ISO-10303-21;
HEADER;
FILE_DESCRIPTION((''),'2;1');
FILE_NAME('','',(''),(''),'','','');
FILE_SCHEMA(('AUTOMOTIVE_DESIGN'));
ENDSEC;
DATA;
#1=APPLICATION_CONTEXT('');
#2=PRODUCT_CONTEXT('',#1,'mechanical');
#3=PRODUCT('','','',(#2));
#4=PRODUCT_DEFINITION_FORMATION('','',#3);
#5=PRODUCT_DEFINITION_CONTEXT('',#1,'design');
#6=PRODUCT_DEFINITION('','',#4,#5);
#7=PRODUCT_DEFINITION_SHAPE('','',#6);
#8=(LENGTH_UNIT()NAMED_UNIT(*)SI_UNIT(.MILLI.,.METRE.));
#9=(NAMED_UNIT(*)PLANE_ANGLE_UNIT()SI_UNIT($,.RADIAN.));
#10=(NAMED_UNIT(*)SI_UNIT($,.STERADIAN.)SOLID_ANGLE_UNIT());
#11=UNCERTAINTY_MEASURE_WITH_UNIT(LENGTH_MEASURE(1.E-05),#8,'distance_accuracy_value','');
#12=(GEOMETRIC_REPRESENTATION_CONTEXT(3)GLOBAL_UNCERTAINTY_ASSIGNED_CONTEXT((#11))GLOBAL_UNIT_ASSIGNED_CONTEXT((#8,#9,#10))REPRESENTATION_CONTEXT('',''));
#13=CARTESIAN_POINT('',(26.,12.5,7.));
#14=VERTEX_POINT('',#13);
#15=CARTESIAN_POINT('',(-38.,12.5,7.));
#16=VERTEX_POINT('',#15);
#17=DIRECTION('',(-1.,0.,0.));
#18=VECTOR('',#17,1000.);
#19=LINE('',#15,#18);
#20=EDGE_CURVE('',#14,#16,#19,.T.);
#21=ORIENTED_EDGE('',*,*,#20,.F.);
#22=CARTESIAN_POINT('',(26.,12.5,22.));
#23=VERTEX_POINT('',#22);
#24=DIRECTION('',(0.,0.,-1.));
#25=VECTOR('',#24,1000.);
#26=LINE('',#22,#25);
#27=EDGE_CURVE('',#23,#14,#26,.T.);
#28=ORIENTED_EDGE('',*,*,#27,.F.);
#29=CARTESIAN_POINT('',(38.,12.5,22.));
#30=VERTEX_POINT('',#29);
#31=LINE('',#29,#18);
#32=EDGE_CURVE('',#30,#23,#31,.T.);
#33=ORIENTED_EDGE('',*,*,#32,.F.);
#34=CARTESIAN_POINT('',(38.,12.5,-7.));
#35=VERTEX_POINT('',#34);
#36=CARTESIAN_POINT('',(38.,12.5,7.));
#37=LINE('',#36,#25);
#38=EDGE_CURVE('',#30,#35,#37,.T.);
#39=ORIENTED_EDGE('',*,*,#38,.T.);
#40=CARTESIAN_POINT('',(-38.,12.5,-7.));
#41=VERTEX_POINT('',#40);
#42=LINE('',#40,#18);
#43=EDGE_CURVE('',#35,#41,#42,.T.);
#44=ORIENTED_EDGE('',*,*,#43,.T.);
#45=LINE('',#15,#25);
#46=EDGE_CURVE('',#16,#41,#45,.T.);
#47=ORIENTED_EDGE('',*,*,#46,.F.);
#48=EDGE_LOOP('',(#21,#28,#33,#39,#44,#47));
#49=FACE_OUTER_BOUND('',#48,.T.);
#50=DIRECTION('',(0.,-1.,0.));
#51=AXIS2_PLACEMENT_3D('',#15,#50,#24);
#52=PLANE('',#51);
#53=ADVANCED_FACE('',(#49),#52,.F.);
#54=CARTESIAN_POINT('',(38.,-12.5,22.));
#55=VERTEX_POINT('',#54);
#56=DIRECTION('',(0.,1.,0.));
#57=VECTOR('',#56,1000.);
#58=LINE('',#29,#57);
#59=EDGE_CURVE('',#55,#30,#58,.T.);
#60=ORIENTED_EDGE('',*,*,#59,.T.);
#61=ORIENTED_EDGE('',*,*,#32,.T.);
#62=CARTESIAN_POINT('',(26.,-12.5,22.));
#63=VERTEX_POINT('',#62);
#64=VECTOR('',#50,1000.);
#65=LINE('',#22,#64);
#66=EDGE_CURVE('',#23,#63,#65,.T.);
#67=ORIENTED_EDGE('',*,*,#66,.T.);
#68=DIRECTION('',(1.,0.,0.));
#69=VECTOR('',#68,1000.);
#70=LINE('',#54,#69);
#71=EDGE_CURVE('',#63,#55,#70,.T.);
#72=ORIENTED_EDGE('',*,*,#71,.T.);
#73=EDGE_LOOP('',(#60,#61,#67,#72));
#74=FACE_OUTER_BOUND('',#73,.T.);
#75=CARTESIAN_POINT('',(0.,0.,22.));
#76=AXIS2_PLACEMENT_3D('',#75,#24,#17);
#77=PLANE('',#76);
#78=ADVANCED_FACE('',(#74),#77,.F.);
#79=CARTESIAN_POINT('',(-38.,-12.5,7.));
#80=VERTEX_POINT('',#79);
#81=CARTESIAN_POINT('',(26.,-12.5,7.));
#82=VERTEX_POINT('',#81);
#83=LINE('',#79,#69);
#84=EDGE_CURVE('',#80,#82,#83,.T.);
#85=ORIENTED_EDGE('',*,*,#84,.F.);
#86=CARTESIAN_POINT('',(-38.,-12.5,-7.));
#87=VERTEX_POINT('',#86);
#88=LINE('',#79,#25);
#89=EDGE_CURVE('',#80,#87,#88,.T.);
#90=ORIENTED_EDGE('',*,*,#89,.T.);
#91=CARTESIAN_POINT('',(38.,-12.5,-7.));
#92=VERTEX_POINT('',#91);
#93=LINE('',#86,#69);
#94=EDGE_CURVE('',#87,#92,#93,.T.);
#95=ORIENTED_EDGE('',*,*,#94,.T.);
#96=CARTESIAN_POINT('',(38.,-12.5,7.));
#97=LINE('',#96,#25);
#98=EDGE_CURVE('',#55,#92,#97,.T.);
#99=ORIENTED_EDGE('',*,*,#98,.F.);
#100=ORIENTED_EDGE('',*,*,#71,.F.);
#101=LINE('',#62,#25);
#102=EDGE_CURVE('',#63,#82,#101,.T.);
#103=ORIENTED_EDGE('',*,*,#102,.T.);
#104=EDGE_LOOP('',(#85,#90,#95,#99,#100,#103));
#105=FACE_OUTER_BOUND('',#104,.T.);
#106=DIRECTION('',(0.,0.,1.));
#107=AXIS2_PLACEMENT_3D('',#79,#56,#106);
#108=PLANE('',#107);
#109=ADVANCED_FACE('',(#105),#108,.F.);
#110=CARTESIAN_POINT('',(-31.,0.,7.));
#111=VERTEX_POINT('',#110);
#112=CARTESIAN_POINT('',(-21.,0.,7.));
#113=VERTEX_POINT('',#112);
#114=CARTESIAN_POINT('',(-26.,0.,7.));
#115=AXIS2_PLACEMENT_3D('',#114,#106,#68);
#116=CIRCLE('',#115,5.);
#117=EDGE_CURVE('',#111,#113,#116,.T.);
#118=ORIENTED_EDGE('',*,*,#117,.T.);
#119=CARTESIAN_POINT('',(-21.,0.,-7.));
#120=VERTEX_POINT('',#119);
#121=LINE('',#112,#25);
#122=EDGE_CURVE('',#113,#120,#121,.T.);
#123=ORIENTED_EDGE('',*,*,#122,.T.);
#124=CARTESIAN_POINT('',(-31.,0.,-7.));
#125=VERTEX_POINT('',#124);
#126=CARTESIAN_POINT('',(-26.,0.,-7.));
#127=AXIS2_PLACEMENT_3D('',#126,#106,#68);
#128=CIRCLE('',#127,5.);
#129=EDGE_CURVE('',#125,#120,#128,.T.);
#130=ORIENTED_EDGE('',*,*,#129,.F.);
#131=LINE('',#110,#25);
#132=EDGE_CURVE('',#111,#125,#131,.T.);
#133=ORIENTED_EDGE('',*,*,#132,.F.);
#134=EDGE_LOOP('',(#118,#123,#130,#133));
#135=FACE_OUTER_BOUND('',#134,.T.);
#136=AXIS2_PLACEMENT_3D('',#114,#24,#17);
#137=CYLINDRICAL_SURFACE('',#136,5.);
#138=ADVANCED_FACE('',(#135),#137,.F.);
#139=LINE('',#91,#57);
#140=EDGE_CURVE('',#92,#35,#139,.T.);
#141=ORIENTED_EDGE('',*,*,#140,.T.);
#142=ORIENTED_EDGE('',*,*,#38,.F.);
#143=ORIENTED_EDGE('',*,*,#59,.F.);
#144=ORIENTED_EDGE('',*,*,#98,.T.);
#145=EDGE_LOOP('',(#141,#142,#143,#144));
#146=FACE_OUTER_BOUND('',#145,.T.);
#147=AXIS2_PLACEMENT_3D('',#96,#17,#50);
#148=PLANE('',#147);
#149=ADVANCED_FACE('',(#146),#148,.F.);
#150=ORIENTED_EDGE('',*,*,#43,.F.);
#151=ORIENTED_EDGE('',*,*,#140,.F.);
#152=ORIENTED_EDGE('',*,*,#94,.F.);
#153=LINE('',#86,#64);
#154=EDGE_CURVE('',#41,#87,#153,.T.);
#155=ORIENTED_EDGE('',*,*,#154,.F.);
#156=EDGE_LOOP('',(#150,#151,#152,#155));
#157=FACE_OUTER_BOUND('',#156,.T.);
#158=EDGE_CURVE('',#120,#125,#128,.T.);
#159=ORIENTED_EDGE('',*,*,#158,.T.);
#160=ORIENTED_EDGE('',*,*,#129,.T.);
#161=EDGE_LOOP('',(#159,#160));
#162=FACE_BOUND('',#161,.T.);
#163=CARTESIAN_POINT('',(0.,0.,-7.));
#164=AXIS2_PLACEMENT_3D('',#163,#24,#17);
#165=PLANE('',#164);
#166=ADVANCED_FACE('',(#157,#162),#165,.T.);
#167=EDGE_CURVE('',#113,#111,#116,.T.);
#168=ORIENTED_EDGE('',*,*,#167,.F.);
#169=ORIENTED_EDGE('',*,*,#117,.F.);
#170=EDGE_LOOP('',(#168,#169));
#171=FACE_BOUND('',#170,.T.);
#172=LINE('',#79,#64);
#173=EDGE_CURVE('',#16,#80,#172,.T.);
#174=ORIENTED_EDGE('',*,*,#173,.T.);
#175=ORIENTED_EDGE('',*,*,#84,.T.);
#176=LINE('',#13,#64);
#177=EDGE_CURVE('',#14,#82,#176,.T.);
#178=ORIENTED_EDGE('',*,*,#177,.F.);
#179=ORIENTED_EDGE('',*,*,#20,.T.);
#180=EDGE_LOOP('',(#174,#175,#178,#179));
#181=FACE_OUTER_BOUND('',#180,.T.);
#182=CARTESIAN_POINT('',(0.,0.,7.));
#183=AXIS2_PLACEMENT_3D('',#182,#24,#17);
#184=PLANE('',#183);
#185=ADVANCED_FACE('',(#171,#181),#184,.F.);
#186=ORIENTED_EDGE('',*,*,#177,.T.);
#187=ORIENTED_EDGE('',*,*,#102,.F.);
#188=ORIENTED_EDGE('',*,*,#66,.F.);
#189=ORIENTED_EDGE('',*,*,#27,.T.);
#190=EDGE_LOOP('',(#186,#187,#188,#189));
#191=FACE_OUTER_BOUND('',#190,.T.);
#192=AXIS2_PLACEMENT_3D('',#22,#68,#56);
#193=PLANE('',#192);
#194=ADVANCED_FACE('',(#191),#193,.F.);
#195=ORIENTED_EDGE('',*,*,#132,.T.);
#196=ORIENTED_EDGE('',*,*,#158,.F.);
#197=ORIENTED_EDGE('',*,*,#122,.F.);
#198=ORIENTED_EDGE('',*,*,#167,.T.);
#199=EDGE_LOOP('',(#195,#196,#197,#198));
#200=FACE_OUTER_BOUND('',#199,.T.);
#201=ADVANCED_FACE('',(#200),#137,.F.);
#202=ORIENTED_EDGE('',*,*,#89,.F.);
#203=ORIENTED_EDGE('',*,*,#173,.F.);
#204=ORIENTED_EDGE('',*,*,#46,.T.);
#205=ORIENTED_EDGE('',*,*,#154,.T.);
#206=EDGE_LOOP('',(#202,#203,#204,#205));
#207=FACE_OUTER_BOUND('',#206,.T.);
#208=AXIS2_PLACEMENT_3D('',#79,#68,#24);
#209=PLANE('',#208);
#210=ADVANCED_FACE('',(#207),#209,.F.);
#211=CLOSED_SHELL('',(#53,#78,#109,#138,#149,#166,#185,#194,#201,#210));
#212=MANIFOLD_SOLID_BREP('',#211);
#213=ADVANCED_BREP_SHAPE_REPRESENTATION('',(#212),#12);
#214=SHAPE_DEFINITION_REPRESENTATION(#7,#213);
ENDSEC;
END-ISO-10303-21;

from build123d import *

# Parameters (mm, degrees)
SKETCH_1_W      = 76
SKETCH_1_H      = 25
SKETCH_1_R      = 5
EXTRUDE_1_DEPTH = 7
SKETCH_2_W      = 12
SKETCH_2_H      = 25
EXTRUDE_2_DEPTH = 15


with BuildPart() as part:
    # 草图1 → 凸台-拉伸1 (new, symmetric)
    with BuildSketch(Plane.XY):
        Rectangle(SKETCH_1_W, SKETCH_1_H)
        with Locations((-26, 0)):
            Circle(SKETCH_1_R, mode=Mode.SUBTRACT)
    extrude(amount=EXTRUDE_1_DEPTH, both=True)

    # 草图2 → 凸台-拉伸2 (add)
    with BuildSketch(Plane.XY.offset(7)):
        with Locations((32, 0)):
            Rectangle(SKETCH_2_W, SKETCH_2_H)
    extrude(amount=EXTRUDE_2_DEPTH)


solid = part.part
